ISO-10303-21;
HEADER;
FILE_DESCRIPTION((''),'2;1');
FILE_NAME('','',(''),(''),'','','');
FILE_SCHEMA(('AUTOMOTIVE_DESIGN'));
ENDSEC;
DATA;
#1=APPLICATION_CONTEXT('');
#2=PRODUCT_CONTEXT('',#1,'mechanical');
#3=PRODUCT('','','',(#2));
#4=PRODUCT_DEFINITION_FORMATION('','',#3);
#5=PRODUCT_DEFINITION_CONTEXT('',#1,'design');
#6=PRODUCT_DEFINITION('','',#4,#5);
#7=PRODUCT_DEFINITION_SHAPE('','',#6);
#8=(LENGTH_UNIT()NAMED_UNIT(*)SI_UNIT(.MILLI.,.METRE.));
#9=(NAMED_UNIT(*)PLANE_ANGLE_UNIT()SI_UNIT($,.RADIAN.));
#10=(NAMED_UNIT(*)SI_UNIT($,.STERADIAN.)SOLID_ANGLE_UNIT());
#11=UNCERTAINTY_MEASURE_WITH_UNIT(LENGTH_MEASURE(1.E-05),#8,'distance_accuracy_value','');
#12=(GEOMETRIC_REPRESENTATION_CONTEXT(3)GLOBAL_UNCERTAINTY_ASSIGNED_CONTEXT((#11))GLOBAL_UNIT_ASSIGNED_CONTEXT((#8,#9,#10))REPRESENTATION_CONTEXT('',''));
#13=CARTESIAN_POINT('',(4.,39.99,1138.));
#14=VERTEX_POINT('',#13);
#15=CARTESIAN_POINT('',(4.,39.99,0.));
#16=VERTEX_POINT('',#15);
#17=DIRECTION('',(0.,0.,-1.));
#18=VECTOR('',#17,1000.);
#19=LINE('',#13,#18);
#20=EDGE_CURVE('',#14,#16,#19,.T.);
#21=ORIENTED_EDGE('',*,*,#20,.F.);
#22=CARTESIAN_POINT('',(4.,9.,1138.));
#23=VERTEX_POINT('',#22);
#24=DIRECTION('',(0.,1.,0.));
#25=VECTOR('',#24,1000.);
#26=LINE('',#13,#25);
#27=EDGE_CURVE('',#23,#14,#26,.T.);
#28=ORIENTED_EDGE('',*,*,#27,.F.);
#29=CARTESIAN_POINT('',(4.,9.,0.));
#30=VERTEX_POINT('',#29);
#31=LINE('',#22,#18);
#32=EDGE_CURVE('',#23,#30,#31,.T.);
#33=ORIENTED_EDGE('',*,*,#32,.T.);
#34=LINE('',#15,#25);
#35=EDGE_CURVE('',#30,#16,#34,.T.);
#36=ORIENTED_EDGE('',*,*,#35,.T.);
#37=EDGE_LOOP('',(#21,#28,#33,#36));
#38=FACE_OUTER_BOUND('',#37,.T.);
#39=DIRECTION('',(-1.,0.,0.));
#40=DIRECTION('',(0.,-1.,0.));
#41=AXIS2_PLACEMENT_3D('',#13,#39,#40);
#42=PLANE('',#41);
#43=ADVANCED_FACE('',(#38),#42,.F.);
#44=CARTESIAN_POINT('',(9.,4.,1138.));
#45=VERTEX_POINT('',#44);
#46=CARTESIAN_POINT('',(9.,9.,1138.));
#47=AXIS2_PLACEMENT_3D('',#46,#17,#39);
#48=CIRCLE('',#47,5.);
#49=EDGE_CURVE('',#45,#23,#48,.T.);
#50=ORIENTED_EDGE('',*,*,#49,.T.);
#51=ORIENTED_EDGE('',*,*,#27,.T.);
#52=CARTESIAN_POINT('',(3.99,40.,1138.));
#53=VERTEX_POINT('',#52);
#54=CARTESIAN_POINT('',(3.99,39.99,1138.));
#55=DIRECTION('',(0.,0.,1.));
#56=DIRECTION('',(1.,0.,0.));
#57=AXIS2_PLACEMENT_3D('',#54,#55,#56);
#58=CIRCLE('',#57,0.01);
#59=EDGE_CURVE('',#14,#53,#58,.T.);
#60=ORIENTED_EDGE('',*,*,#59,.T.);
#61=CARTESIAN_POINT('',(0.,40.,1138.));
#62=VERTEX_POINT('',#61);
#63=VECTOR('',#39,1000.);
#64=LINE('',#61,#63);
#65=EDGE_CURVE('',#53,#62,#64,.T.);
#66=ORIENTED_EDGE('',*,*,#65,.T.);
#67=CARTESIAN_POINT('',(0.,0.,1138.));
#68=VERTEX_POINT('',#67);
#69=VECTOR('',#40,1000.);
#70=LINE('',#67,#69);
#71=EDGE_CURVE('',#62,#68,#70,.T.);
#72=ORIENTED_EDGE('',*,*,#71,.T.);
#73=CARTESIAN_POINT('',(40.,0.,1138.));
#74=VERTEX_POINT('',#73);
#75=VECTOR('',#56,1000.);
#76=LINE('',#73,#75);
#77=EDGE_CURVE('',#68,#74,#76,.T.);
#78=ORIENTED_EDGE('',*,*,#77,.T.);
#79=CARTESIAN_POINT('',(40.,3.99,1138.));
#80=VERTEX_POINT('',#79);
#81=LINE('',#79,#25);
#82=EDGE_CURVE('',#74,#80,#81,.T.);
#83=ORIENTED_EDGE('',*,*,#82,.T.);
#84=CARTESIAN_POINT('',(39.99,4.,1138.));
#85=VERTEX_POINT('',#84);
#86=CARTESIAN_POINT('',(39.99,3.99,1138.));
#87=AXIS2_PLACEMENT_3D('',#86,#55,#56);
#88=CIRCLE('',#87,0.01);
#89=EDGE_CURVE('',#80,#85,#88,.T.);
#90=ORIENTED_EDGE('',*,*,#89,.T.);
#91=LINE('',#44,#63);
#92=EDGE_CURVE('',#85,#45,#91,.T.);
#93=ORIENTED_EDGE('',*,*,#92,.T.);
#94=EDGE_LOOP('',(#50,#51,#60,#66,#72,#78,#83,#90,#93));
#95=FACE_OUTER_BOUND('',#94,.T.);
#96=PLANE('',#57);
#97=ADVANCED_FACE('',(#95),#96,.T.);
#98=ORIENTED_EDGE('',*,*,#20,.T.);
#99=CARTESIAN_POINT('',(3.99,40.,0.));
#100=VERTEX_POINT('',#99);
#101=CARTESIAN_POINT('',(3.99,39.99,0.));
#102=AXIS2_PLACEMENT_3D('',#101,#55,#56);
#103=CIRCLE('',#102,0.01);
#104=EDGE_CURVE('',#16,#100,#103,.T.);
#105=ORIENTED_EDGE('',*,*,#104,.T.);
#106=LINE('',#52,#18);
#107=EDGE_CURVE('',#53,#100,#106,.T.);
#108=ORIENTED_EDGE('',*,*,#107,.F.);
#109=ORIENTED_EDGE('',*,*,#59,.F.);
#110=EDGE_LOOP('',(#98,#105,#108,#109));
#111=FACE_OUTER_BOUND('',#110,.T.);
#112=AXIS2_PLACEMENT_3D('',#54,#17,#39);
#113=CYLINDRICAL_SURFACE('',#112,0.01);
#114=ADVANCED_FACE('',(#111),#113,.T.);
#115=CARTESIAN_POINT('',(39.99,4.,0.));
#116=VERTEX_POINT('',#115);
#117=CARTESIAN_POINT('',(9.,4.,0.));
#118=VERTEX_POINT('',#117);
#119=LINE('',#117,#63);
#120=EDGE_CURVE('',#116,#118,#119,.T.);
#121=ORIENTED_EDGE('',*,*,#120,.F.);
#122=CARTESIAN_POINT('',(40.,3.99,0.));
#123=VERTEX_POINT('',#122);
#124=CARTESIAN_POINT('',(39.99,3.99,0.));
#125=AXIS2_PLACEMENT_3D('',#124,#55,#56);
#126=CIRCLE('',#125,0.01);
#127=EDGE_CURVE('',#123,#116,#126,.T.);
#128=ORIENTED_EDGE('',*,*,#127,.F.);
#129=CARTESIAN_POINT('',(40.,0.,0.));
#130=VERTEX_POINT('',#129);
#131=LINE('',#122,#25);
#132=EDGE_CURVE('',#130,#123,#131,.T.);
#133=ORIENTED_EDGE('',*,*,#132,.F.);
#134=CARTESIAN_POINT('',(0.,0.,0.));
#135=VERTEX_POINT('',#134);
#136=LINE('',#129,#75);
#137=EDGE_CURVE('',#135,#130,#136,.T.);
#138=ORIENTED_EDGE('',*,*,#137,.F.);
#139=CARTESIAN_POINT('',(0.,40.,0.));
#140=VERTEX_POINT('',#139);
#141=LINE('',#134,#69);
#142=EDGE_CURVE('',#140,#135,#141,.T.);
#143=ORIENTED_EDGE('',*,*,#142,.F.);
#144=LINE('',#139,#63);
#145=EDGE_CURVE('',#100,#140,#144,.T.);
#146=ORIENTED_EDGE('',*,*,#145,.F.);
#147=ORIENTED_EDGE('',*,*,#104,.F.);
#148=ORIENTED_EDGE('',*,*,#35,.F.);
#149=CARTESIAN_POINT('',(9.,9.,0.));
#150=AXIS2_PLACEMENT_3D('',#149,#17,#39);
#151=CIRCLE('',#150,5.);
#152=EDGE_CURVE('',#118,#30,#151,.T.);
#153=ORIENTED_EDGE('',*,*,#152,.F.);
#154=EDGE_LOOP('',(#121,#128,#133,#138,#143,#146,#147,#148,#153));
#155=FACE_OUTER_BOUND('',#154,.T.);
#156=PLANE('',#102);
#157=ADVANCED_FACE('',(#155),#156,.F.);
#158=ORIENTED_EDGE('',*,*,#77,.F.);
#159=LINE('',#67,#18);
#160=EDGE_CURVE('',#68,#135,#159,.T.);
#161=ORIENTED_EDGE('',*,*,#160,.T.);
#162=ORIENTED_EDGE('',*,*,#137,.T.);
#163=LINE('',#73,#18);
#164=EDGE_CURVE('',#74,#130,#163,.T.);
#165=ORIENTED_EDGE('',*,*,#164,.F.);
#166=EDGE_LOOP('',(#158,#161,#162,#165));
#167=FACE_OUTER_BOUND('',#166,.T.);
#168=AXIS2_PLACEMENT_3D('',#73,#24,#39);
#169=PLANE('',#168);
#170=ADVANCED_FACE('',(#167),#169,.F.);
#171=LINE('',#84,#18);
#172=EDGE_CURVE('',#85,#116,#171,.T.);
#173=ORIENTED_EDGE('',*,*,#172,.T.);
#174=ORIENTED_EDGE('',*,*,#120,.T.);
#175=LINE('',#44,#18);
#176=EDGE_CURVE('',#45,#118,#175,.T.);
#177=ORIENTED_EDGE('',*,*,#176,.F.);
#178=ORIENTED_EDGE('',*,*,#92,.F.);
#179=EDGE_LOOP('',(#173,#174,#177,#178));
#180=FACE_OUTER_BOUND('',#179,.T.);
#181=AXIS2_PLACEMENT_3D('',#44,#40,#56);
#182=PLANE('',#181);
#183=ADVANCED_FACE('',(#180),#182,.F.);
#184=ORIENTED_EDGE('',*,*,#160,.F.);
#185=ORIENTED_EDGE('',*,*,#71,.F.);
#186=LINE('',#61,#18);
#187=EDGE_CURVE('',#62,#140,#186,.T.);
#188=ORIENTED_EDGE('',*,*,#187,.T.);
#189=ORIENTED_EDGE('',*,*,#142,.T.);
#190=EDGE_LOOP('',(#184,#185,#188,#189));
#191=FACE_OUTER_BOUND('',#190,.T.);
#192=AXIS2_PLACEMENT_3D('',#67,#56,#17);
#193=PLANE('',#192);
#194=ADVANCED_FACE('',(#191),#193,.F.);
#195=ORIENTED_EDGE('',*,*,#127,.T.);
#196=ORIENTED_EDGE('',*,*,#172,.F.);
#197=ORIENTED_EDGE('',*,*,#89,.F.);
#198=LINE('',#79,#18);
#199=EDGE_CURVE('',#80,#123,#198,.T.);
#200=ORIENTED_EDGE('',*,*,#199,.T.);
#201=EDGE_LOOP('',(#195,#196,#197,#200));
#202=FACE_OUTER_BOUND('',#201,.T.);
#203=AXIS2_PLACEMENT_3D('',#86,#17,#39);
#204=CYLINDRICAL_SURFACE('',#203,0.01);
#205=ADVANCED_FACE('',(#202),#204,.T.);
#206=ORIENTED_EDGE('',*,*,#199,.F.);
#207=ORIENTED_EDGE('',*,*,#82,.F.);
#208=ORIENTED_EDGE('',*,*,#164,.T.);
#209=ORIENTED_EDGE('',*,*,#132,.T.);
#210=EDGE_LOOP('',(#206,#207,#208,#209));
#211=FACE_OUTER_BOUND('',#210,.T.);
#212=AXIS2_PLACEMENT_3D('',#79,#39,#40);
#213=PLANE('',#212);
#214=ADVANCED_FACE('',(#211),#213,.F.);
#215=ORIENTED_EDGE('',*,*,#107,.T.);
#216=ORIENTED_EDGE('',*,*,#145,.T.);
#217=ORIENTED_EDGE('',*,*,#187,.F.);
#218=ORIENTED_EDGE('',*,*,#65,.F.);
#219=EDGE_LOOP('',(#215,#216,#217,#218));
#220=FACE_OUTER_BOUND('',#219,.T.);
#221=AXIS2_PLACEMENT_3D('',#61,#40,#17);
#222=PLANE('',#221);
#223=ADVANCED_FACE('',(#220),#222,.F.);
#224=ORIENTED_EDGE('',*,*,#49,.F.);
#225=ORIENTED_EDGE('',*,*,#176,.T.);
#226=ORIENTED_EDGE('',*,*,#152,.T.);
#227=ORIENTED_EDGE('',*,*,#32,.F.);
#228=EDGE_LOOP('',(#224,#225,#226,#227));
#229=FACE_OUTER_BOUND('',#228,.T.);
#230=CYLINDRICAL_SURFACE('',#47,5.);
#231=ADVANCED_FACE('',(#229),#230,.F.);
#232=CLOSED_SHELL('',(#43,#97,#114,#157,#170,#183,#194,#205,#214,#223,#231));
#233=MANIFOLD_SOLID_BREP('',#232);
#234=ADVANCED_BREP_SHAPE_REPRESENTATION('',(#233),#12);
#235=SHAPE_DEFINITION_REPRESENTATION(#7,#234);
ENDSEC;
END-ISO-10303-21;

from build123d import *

# Parameters (mm, degrees)
EXTRUDE_1_DEPTH = 1138


with BuildPart() as part:
    # 草图1 → 拉伸1 (new body)
    with BuildSketch(Plane.XY):
        with BuildLine():
            Line((0, 0), (0, 40))
            Line((0, 40), (3.99, 40))
            ThreePointArc((3.99, 40), (3.997071068, 39.997071068), (4, 39.99))
            Line((4, 39.99), (4, 9))
            ThreePointArc((4, 9), (5.464466094, 5.464466094), (9, 4))
            Line((9, 4), (39.99, 4))
            ThreePointArc((39.99, 4), (39.997071068, 3.997071068), (40, 3.99))
            Line((40, 3.99), (40, 0))
            Line((40, 0), (0, 0))
        make_face()
    extrude(amount=EXTRUDE_1_DEPTH)


solid = part.part
